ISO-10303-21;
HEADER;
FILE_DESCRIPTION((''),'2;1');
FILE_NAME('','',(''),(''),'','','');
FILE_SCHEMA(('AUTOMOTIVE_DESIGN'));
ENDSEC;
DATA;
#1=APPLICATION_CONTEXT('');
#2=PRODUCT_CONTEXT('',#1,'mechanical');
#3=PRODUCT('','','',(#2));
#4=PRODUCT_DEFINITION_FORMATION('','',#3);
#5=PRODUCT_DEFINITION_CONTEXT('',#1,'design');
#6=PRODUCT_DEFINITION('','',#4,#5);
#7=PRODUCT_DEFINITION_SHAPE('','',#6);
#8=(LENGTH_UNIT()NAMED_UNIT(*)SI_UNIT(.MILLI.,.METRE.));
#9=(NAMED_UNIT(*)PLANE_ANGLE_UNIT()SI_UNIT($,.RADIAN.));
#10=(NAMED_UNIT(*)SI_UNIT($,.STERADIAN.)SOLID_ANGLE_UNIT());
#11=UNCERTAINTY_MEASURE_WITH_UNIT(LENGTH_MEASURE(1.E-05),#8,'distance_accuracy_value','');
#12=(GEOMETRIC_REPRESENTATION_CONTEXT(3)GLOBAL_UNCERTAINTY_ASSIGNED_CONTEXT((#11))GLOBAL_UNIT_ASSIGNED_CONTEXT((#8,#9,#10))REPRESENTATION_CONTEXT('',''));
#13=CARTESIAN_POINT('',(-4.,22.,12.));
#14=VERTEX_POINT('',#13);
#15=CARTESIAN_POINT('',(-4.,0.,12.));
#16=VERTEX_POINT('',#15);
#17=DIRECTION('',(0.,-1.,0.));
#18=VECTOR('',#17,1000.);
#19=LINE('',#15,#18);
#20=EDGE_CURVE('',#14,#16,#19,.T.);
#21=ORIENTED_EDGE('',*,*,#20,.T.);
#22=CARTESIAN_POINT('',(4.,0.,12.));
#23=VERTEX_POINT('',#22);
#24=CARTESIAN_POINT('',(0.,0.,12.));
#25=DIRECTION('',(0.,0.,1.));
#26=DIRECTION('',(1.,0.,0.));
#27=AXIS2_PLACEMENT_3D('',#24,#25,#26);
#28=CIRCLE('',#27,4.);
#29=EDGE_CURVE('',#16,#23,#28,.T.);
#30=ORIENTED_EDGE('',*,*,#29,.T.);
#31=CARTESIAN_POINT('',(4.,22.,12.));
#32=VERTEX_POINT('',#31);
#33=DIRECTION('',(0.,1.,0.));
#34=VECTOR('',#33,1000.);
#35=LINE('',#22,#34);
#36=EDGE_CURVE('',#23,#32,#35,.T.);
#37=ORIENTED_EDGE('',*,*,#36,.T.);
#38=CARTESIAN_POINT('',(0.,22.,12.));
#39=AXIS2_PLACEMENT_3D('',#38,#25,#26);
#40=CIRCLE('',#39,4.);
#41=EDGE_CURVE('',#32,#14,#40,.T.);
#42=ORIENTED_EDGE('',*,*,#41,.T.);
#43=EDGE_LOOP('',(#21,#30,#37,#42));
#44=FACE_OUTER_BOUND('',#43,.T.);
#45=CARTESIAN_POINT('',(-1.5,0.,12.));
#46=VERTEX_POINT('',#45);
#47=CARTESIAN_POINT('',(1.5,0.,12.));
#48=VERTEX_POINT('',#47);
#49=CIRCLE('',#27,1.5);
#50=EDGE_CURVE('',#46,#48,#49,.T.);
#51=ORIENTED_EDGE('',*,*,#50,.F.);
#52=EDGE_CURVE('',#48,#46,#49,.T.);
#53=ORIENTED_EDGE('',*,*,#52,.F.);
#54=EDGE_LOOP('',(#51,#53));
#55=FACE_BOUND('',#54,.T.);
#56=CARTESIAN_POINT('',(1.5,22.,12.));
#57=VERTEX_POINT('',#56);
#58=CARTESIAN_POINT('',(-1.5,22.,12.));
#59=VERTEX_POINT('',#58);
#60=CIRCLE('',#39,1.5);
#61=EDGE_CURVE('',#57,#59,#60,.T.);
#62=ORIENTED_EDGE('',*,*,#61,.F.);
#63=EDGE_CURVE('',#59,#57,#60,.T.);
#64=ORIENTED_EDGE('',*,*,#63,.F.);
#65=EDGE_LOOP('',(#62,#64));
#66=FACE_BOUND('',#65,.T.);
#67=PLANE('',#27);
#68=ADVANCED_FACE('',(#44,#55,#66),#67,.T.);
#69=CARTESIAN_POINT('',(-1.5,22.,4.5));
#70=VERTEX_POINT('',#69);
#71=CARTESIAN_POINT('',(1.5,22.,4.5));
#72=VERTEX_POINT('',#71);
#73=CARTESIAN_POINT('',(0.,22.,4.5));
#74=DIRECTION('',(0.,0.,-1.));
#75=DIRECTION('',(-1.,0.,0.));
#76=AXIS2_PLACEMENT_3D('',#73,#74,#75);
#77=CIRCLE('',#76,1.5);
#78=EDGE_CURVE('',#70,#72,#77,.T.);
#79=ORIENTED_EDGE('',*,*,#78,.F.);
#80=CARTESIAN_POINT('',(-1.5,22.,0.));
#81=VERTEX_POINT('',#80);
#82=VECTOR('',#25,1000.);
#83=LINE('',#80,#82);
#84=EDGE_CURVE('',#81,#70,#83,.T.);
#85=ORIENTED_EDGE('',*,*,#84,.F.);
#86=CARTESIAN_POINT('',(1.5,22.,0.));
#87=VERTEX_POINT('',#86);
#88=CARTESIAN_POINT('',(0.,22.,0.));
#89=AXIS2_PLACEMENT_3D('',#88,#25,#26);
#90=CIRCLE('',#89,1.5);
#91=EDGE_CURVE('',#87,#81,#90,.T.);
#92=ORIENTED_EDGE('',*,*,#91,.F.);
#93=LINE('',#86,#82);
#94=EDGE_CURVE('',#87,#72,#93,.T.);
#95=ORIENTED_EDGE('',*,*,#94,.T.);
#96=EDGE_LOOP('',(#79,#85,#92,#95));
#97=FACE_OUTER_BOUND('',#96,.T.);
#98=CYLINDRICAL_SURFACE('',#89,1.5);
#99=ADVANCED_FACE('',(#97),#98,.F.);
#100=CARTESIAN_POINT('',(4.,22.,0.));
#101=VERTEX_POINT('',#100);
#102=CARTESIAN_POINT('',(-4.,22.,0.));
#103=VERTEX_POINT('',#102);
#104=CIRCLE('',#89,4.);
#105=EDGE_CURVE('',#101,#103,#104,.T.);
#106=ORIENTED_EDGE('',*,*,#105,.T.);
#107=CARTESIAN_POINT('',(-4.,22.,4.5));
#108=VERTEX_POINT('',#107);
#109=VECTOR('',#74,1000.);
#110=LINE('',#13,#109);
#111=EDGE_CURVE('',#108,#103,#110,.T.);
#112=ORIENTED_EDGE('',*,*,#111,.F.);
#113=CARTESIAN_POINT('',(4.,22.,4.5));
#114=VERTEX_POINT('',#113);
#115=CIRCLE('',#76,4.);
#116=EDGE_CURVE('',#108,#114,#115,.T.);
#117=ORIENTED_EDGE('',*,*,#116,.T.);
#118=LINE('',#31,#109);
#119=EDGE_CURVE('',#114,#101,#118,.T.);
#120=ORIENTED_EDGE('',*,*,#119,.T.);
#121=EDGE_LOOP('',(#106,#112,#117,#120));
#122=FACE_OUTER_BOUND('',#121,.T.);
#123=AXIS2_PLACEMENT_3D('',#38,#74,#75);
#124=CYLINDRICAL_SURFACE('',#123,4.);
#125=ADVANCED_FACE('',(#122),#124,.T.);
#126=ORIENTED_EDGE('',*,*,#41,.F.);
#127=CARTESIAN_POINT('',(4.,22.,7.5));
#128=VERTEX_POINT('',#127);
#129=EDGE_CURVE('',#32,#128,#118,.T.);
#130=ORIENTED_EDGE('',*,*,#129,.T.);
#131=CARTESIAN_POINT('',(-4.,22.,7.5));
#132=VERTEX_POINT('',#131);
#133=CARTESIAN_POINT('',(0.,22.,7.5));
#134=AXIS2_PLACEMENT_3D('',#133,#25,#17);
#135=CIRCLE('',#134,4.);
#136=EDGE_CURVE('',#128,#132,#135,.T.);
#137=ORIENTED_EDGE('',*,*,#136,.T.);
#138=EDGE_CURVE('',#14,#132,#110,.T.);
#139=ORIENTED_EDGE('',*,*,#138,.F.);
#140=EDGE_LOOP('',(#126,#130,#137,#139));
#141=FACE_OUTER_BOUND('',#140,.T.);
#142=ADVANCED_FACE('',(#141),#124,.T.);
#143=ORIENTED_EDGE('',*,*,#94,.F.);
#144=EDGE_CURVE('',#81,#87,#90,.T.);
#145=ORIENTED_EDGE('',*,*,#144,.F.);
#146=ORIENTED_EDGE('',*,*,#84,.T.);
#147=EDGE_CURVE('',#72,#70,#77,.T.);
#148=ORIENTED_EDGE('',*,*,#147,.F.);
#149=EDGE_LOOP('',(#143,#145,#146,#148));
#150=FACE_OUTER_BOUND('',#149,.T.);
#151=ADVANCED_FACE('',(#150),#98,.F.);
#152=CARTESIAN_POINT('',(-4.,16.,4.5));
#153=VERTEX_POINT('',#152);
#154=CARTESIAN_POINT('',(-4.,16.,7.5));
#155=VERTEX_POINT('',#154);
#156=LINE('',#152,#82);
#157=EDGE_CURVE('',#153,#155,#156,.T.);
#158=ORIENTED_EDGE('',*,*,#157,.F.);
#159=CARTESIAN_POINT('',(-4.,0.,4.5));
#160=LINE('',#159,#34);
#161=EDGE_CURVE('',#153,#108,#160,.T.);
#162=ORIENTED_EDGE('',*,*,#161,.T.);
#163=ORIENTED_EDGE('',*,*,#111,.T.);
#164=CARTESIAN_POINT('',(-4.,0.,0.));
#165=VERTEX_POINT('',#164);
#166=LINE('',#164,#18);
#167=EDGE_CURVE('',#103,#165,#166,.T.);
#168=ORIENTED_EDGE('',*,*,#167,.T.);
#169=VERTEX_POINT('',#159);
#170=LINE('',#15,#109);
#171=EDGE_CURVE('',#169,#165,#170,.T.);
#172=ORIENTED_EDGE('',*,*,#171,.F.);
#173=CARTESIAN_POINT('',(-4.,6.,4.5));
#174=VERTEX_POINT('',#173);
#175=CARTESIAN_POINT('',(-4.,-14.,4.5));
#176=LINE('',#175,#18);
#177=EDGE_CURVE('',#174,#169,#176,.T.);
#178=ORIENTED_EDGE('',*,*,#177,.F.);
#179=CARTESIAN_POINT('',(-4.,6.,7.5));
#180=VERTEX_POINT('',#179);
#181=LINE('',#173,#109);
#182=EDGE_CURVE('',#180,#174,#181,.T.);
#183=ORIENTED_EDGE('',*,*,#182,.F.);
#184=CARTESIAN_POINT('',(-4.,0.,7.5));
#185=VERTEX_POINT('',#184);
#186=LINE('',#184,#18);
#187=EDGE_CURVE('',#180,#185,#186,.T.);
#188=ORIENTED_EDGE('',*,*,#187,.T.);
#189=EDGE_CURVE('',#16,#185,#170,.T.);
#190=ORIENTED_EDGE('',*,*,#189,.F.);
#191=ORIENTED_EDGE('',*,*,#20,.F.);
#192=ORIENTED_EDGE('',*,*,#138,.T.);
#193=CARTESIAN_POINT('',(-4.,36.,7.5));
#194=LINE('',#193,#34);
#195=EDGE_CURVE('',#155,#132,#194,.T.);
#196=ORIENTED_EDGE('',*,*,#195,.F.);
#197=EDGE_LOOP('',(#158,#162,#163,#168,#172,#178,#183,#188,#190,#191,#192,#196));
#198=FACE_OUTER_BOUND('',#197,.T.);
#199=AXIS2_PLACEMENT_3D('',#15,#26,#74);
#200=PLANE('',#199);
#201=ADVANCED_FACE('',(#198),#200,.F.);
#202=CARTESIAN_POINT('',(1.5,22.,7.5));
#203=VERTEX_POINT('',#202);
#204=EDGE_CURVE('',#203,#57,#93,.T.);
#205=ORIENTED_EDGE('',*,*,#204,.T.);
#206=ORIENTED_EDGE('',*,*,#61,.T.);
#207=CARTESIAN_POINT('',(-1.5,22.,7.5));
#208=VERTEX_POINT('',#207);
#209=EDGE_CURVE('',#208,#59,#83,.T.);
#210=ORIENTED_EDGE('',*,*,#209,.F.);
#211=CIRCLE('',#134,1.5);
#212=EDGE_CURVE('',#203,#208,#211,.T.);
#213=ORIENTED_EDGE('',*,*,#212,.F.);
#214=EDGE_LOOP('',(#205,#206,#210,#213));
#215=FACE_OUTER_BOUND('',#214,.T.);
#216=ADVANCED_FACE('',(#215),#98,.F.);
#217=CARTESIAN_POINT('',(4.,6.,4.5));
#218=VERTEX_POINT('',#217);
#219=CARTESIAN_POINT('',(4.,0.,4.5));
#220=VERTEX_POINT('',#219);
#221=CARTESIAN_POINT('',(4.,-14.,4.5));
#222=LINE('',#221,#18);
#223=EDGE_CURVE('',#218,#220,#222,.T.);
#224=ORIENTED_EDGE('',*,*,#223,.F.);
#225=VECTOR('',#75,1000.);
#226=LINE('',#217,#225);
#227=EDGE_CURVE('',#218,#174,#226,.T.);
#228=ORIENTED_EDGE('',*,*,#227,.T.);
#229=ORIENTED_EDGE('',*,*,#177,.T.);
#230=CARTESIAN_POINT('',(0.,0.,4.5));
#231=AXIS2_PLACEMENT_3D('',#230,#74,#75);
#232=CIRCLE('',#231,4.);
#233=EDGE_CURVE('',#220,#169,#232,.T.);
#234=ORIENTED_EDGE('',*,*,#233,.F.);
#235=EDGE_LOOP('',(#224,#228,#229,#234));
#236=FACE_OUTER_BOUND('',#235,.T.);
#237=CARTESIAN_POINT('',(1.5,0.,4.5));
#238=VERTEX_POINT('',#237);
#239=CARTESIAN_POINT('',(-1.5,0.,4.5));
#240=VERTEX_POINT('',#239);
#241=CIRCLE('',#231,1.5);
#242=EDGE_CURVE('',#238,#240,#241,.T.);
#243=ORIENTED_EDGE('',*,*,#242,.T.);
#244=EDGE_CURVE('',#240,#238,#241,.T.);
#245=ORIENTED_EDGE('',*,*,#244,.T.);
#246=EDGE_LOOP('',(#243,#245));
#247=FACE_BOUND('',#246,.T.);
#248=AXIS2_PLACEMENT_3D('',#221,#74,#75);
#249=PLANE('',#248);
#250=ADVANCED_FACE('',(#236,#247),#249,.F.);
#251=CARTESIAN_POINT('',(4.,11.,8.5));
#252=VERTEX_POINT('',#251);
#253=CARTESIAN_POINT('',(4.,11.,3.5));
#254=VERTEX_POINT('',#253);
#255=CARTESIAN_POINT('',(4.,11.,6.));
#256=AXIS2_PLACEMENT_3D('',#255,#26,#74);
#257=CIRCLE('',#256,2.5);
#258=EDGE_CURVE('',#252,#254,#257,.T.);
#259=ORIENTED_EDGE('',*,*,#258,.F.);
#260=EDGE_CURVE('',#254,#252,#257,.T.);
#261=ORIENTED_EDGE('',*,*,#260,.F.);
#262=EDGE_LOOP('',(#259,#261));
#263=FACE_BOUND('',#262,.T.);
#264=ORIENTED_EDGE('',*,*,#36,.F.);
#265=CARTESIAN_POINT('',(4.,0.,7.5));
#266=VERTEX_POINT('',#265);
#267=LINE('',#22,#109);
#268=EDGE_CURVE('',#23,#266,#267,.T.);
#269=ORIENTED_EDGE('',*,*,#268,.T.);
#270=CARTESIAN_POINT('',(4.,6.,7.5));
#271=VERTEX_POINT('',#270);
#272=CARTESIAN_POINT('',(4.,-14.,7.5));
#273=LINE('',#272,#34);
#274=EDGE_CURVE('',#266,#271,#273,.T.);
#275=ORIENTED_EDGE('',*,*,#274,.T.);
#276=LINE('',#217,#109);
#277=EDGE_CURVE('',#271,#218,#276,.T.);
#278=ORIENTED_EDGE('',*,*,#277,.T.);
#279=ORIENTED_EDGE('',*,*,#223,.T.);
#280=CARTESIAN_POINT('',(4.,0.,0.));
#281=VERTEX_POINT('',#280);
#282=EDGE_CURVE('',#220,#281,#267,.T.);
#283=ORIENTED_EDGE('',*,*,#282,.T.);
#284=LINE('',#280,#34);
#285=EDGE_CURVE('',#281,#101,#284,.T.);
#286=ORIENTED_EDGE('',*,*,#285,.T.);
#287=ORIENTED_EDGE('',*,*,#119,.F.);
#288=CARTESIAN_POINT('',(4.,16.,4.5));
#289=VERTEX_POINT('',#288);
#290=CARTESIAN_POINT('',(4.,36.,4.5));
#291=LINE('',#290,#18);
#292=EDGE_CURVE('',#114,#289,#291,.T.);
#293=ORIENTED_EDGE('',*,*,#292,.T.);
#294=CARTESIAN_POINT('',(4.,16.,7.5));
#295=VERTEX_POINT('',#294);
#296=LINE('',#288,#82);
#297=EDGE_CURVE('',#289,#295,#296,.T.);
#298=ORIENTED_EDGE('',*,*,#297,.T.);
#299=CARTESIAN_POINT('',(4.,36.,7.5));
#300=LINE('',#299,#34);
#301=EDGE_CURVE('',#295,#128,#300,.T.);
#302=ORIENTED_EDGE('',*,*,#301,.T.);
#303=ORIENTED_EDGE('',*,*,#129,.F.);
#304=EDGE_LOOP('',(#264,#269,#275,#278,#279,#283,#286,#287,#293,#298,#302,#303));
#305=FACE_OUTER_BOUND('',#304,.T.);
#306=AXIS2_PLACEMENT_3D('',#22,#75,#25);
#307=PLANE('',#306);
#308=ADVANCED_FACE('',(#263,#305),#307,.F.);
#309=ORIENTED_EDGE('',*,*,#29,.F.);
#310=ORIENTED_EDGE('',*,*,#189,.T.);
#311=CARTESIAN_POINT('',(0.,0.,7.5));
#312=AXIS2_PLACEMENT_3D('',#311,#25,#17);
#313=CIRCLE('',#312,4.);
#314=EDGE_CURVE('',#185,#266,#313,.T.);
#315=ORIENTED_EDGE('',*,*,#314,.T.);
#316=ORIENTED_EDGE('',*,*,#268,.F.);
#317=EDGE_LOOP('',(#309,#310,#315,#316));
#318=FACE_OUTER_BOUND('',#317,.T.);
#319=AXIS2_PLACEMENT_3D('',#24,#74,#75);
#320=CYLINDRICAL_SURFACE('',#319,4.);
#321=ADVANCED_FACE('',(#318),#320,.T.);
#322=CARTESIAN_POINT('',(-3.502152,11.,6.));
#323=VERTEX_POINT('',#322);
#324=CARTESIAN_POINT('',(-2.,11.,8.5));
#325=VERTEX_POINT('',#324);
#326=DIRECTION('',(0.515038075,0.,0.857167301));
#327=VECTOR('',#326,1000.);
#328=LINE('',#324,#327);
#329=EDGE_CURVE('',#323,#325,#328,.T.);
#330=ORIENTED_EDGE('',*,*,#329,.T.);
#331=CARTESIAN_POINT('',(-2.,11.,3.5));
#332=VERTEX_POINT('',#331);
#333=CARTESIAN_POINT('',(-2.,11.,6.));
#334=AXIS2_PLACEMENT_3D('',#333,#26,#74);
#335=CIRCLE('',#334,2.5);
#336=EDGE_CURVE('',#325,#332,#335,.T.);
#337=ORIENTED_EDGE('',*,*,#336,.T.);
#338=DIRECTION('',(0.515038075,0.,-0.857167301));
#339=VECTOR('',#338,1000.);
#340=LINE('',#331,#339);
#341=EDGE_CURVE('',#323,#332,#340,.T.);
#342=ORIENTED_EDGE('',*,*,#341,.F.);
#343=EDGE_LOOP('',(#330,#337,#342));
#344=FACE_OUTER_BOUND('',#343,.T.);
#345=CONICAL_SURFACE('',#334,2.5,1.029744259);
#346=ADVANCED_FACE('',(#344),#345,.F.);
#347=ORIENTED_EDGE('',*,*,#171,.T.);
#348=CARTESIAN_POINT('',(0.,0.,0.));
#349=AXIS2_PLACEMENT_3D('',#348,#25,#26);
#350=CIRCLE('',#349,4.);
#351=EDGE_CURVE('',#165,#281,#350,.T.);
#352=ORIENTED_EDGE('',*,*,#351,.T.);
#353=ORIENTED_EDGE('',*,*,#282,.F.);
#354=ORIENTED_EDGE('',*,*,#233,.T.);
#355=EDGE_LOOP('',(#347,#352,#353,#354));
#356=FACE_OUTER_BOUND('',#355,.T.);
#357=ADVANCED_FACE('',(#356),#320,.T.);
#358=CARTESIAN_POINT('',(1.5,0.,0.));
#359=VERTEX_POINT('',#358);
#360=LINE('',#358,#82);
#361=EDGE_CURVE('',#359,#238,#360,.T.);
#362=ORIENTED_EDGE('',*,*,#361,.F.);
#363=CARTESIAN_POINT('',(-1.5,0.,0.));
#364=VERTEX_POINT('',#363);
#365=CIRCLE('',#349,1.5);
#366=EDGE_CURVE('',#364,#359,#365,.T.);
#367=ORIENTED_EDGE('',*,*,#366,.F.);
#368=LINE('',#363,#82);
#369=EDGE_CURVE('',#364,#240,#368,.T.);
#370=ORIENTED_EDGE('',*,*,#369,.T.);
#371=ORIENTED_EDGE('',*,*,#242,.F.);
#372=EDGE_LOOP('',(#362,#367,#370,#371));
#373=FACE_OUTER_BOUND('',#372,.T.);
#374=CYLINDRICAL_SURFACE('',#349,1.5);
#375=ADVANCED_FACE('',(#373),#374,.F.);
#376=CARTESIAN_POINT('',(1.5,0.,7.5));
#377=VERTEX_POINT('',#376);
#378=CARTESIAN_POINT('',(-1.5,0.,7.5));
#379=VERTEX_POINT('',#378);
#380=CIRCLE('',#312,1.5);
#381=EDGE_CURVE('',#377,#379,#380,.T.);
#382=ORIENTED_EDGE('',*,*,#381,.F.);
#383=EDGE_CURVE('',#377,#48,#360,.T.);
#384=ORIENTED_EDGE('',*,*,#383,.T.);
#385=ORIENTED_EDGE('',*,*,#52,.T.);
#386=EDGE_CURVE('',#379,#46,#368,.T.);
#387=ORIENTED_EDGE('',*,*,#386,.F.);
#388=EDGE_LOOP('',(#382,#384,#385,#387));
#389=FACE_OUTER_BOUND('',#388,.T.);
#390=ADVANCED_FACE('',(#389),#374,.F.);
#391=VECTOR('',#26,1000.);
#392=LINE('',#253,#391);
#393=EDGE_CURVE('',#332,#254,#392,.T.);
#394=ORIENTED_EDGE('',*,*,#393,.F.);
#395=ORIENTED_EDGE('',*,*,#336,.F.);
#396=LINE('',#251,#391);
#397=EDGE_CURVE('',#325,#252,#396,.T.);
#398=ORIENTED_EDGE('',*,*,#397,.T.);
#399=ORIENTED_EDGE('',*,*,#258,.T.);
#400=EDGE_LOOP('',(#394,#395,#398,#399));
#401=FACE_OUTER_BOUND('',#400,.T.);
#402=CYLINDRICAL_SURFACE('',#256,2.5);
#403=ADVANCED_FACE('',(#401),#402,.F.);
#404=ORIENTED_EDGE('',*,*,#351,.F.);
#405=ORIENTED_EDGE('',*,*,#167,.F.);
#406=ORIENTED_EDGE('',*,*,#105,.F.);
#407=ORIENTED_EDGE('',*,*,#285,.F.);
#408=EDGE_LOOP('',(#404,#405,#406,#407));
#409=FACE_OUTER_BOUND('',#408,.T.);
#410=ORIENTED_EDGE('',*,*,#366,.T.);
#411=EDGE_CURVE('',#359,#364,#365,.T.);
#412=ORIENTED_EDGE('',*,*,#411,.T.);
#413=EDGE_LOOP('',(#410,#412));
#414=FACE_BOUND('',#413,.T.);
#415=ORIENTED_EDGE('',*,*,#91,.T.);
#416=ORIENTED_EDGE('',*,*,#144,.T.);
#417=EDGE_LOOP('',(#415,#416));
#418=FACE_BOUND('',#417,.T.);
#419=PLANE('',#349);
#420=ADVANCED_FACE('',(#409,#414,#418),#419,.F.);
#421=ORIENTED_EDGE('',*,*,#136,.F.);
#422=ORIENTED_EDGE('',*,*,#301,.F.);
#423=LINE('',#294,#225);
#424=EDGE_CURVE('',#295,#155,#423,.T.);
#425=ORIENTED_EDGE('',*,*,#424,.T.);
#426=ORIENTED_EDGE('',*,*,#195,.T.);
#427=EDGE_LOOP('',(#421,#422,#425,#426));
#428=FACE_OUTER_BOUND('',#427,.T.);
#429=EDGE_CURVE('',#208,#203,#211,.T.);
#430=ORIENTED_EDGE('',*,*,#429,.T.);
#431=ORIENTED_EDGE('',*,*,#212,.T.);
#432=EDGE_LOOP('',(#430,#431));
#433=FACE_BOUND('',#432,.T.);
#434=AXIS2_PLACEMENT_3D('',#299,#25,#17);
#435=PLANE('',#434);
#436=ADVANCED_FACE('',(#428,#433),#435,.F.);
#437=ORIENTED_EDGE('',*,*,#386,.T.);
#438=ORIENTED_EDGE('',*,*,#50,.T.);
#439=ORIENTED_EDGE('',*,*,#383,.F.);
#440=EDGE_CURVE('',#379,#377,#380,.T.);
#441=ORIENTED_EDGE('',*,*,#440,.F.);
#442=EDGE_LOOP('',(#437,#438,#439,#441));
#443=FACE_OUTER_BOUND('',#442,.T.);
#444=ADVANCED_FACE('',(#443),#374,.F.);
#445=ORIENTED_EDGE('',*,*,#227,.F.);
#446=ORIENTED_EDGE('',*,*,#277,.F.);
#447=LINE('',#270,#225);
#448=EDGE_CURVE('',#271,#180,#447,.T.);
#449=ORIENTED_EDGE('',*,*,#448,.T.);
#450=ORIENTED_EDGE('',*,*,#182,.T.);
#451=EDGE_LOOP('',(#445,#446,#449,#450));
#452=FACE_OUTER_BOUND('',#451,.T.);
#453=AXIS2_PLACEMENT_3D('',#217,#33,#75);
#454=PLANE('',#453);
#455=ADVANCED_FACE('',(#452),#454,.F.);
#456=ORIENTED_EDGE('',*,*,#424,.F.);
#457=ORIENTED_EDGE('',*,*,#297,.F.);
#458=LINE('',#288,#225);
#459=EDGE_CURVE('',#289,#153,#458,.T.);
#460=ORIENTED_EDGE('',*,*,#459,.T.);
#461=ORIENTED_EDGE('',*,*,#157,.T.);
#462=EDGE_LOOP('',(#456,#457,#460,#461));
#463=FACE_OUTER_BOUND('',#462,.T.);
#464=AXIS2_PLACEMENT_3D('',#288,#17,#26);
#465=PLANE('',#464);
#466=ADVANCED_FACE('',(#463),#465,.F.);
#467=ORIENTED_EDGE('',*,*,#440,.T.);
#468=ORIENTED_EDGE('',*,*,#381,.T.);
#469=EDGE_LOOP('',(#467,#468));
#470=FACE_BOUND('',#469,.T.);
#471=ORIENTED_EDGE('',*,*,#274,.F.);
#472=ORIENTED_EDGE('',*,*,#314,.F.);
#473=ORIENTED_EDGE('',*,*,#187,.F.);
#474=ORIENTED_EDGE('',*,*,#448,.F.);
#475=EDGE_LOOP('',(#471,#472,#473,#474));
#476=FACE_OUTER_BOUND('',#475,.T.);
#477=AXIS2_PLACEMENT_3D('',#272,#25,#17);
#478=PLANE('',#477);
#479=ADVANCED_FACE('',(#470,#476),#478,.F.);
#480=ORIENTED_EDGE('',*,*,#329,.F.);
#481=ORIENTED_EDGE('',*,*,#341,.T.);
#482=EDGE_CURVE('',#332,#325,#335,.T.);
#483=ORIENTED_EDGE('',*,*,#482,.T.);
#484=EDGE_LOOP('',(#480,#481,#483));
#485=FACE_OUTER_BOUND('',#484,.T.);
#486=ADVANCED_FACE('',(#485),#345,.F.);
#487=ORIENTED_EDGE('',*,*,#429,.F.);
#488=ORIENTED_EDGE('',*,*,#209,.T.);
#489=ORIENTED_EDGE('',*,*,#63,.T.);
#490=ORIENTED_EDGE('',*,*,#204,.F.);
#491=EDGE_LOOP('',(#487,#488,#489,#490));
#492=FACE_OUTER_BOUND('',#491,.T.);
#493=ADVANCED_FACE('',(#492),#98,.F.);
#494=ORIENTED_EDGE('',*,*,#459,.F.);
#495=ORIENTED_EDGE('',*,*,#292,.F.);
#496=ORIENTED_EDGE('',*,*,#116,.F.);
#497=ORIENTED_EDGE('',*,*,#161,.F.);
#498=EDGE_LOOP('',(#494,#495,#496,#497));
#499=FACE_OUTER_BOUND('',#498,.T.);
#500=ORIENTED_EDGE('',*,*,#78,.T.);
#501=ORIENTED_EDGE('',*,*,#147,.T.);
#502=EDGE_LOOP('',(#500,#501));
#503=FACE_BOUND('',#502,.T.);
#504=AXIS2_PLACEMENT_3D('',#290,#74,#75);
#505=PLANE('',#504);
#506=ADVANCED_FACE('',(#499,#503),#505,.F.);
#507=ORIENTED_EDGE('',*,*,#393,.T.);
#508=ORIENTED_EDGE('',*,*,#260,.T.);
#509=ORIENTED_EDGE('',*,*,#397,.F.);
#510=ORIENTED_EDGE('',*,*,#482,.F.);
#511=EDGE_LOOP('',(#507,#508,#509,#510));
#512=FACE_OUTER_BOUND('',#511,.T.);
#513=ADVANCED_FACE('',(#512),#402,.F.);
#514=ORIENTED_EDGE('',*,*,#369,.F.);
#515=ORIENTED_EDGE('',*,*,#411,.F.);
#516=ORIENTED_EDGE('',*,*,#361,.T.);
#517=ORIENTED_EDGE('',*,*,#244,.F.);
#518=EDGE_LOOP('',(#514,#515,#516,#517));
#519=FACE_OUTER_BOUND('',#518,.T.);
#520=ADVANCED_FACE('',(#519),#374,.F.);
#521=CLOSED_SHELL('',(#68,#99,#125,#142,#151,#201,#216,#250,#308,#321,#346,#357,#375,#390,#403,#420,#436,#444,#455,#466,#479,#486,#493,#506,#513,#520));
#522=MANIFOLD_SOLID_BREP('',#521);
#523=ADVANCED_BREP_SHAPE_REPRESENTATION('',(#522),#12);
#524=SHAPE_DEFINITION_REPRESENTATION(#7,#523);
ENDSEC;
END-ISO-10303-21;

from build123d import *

# Parameters (mm, degrees)
BOSS_EXTRUDE1_DEPTH   = 12
SKETCH2_W             = 3
SKETCH2_H             = 20
CUT_EXTRUDE1_DEPTH    = 30.732137495
SKETCH3_R             = 1.5
CUT_EXTRUDE2_DEPTH    = 29.91366459
M6_TAPPED_HOLE1_D     = 5
M6_TAPPED_HOLE1_DEPTH = 6
M6_TAPPED_HOLE1_TIP   = 1.502151548


with BuildPart() as part:
    # Sketch1 → Boss-Extrude1 (new body)
    with BuildSketch(Plane.XY):
        with BuildLine():
            Line((-4, 0), (-4, 22))
            ThreePointArc((-4, 22), (0, 26), (4, 22))
            Line((4, 22), (4, 0))
            ThreePointArc((4, 0), (0, -4), (-4, 0))
        make_face()
    extrude(amount=BOSS_EXTRUDE1_DEPTH)

    # Sketch2 → Cut-Extrude1 (cut, through all)
    with BuildSketch(Plane.ZY.offset(4)):
        with Locations((6, 26)):
            Rectangle(SKETCH2_W, SKETCH2_H)
        with Locations((6, -4)):
            Rectangle(SKETCH2_W, SKETCH2_H)
    extrude(amount=-CUT_EXTRUDE1_DEPTH, mode=Mode.SUBTRACT)

    # Sketch3 → Cut-Extrude2 (cut, through all)
    with BuildSketch(Plane.XY.offset(12)):
        with Locations((0, 22)):
            Circle(SKETCH3_R)
        Circle(SKETCH3_R)
    extrude(amount=-CUT_EXTRUDE2_DEPTH, mode=Mode.SUBTRACT)

    # M6 Tapped Hole1
    with Locations(Plane(origin=(4, 11, 6), x_dir=(0, 0, 1), z_dir=(1, 0, 0))):
        with Locations((0, 0)):
            Hole(M6_TAPPED_HOLE1_D / 2, depth=M6_TAPPED_HOLE1_DEPTH)
            with Locations((0, 0, -(M6_TAPPED_HOLE1_DEPTH + M6_TAPPED_HOLE1_TIP / 2))):  # 118° drill point
                Cone(0, M6_TAPPED_HOLE1_D / 2, M6_TAPPED_HOLE1_TIP, mode=Mode.SUBTRACT)


solid = part.part
